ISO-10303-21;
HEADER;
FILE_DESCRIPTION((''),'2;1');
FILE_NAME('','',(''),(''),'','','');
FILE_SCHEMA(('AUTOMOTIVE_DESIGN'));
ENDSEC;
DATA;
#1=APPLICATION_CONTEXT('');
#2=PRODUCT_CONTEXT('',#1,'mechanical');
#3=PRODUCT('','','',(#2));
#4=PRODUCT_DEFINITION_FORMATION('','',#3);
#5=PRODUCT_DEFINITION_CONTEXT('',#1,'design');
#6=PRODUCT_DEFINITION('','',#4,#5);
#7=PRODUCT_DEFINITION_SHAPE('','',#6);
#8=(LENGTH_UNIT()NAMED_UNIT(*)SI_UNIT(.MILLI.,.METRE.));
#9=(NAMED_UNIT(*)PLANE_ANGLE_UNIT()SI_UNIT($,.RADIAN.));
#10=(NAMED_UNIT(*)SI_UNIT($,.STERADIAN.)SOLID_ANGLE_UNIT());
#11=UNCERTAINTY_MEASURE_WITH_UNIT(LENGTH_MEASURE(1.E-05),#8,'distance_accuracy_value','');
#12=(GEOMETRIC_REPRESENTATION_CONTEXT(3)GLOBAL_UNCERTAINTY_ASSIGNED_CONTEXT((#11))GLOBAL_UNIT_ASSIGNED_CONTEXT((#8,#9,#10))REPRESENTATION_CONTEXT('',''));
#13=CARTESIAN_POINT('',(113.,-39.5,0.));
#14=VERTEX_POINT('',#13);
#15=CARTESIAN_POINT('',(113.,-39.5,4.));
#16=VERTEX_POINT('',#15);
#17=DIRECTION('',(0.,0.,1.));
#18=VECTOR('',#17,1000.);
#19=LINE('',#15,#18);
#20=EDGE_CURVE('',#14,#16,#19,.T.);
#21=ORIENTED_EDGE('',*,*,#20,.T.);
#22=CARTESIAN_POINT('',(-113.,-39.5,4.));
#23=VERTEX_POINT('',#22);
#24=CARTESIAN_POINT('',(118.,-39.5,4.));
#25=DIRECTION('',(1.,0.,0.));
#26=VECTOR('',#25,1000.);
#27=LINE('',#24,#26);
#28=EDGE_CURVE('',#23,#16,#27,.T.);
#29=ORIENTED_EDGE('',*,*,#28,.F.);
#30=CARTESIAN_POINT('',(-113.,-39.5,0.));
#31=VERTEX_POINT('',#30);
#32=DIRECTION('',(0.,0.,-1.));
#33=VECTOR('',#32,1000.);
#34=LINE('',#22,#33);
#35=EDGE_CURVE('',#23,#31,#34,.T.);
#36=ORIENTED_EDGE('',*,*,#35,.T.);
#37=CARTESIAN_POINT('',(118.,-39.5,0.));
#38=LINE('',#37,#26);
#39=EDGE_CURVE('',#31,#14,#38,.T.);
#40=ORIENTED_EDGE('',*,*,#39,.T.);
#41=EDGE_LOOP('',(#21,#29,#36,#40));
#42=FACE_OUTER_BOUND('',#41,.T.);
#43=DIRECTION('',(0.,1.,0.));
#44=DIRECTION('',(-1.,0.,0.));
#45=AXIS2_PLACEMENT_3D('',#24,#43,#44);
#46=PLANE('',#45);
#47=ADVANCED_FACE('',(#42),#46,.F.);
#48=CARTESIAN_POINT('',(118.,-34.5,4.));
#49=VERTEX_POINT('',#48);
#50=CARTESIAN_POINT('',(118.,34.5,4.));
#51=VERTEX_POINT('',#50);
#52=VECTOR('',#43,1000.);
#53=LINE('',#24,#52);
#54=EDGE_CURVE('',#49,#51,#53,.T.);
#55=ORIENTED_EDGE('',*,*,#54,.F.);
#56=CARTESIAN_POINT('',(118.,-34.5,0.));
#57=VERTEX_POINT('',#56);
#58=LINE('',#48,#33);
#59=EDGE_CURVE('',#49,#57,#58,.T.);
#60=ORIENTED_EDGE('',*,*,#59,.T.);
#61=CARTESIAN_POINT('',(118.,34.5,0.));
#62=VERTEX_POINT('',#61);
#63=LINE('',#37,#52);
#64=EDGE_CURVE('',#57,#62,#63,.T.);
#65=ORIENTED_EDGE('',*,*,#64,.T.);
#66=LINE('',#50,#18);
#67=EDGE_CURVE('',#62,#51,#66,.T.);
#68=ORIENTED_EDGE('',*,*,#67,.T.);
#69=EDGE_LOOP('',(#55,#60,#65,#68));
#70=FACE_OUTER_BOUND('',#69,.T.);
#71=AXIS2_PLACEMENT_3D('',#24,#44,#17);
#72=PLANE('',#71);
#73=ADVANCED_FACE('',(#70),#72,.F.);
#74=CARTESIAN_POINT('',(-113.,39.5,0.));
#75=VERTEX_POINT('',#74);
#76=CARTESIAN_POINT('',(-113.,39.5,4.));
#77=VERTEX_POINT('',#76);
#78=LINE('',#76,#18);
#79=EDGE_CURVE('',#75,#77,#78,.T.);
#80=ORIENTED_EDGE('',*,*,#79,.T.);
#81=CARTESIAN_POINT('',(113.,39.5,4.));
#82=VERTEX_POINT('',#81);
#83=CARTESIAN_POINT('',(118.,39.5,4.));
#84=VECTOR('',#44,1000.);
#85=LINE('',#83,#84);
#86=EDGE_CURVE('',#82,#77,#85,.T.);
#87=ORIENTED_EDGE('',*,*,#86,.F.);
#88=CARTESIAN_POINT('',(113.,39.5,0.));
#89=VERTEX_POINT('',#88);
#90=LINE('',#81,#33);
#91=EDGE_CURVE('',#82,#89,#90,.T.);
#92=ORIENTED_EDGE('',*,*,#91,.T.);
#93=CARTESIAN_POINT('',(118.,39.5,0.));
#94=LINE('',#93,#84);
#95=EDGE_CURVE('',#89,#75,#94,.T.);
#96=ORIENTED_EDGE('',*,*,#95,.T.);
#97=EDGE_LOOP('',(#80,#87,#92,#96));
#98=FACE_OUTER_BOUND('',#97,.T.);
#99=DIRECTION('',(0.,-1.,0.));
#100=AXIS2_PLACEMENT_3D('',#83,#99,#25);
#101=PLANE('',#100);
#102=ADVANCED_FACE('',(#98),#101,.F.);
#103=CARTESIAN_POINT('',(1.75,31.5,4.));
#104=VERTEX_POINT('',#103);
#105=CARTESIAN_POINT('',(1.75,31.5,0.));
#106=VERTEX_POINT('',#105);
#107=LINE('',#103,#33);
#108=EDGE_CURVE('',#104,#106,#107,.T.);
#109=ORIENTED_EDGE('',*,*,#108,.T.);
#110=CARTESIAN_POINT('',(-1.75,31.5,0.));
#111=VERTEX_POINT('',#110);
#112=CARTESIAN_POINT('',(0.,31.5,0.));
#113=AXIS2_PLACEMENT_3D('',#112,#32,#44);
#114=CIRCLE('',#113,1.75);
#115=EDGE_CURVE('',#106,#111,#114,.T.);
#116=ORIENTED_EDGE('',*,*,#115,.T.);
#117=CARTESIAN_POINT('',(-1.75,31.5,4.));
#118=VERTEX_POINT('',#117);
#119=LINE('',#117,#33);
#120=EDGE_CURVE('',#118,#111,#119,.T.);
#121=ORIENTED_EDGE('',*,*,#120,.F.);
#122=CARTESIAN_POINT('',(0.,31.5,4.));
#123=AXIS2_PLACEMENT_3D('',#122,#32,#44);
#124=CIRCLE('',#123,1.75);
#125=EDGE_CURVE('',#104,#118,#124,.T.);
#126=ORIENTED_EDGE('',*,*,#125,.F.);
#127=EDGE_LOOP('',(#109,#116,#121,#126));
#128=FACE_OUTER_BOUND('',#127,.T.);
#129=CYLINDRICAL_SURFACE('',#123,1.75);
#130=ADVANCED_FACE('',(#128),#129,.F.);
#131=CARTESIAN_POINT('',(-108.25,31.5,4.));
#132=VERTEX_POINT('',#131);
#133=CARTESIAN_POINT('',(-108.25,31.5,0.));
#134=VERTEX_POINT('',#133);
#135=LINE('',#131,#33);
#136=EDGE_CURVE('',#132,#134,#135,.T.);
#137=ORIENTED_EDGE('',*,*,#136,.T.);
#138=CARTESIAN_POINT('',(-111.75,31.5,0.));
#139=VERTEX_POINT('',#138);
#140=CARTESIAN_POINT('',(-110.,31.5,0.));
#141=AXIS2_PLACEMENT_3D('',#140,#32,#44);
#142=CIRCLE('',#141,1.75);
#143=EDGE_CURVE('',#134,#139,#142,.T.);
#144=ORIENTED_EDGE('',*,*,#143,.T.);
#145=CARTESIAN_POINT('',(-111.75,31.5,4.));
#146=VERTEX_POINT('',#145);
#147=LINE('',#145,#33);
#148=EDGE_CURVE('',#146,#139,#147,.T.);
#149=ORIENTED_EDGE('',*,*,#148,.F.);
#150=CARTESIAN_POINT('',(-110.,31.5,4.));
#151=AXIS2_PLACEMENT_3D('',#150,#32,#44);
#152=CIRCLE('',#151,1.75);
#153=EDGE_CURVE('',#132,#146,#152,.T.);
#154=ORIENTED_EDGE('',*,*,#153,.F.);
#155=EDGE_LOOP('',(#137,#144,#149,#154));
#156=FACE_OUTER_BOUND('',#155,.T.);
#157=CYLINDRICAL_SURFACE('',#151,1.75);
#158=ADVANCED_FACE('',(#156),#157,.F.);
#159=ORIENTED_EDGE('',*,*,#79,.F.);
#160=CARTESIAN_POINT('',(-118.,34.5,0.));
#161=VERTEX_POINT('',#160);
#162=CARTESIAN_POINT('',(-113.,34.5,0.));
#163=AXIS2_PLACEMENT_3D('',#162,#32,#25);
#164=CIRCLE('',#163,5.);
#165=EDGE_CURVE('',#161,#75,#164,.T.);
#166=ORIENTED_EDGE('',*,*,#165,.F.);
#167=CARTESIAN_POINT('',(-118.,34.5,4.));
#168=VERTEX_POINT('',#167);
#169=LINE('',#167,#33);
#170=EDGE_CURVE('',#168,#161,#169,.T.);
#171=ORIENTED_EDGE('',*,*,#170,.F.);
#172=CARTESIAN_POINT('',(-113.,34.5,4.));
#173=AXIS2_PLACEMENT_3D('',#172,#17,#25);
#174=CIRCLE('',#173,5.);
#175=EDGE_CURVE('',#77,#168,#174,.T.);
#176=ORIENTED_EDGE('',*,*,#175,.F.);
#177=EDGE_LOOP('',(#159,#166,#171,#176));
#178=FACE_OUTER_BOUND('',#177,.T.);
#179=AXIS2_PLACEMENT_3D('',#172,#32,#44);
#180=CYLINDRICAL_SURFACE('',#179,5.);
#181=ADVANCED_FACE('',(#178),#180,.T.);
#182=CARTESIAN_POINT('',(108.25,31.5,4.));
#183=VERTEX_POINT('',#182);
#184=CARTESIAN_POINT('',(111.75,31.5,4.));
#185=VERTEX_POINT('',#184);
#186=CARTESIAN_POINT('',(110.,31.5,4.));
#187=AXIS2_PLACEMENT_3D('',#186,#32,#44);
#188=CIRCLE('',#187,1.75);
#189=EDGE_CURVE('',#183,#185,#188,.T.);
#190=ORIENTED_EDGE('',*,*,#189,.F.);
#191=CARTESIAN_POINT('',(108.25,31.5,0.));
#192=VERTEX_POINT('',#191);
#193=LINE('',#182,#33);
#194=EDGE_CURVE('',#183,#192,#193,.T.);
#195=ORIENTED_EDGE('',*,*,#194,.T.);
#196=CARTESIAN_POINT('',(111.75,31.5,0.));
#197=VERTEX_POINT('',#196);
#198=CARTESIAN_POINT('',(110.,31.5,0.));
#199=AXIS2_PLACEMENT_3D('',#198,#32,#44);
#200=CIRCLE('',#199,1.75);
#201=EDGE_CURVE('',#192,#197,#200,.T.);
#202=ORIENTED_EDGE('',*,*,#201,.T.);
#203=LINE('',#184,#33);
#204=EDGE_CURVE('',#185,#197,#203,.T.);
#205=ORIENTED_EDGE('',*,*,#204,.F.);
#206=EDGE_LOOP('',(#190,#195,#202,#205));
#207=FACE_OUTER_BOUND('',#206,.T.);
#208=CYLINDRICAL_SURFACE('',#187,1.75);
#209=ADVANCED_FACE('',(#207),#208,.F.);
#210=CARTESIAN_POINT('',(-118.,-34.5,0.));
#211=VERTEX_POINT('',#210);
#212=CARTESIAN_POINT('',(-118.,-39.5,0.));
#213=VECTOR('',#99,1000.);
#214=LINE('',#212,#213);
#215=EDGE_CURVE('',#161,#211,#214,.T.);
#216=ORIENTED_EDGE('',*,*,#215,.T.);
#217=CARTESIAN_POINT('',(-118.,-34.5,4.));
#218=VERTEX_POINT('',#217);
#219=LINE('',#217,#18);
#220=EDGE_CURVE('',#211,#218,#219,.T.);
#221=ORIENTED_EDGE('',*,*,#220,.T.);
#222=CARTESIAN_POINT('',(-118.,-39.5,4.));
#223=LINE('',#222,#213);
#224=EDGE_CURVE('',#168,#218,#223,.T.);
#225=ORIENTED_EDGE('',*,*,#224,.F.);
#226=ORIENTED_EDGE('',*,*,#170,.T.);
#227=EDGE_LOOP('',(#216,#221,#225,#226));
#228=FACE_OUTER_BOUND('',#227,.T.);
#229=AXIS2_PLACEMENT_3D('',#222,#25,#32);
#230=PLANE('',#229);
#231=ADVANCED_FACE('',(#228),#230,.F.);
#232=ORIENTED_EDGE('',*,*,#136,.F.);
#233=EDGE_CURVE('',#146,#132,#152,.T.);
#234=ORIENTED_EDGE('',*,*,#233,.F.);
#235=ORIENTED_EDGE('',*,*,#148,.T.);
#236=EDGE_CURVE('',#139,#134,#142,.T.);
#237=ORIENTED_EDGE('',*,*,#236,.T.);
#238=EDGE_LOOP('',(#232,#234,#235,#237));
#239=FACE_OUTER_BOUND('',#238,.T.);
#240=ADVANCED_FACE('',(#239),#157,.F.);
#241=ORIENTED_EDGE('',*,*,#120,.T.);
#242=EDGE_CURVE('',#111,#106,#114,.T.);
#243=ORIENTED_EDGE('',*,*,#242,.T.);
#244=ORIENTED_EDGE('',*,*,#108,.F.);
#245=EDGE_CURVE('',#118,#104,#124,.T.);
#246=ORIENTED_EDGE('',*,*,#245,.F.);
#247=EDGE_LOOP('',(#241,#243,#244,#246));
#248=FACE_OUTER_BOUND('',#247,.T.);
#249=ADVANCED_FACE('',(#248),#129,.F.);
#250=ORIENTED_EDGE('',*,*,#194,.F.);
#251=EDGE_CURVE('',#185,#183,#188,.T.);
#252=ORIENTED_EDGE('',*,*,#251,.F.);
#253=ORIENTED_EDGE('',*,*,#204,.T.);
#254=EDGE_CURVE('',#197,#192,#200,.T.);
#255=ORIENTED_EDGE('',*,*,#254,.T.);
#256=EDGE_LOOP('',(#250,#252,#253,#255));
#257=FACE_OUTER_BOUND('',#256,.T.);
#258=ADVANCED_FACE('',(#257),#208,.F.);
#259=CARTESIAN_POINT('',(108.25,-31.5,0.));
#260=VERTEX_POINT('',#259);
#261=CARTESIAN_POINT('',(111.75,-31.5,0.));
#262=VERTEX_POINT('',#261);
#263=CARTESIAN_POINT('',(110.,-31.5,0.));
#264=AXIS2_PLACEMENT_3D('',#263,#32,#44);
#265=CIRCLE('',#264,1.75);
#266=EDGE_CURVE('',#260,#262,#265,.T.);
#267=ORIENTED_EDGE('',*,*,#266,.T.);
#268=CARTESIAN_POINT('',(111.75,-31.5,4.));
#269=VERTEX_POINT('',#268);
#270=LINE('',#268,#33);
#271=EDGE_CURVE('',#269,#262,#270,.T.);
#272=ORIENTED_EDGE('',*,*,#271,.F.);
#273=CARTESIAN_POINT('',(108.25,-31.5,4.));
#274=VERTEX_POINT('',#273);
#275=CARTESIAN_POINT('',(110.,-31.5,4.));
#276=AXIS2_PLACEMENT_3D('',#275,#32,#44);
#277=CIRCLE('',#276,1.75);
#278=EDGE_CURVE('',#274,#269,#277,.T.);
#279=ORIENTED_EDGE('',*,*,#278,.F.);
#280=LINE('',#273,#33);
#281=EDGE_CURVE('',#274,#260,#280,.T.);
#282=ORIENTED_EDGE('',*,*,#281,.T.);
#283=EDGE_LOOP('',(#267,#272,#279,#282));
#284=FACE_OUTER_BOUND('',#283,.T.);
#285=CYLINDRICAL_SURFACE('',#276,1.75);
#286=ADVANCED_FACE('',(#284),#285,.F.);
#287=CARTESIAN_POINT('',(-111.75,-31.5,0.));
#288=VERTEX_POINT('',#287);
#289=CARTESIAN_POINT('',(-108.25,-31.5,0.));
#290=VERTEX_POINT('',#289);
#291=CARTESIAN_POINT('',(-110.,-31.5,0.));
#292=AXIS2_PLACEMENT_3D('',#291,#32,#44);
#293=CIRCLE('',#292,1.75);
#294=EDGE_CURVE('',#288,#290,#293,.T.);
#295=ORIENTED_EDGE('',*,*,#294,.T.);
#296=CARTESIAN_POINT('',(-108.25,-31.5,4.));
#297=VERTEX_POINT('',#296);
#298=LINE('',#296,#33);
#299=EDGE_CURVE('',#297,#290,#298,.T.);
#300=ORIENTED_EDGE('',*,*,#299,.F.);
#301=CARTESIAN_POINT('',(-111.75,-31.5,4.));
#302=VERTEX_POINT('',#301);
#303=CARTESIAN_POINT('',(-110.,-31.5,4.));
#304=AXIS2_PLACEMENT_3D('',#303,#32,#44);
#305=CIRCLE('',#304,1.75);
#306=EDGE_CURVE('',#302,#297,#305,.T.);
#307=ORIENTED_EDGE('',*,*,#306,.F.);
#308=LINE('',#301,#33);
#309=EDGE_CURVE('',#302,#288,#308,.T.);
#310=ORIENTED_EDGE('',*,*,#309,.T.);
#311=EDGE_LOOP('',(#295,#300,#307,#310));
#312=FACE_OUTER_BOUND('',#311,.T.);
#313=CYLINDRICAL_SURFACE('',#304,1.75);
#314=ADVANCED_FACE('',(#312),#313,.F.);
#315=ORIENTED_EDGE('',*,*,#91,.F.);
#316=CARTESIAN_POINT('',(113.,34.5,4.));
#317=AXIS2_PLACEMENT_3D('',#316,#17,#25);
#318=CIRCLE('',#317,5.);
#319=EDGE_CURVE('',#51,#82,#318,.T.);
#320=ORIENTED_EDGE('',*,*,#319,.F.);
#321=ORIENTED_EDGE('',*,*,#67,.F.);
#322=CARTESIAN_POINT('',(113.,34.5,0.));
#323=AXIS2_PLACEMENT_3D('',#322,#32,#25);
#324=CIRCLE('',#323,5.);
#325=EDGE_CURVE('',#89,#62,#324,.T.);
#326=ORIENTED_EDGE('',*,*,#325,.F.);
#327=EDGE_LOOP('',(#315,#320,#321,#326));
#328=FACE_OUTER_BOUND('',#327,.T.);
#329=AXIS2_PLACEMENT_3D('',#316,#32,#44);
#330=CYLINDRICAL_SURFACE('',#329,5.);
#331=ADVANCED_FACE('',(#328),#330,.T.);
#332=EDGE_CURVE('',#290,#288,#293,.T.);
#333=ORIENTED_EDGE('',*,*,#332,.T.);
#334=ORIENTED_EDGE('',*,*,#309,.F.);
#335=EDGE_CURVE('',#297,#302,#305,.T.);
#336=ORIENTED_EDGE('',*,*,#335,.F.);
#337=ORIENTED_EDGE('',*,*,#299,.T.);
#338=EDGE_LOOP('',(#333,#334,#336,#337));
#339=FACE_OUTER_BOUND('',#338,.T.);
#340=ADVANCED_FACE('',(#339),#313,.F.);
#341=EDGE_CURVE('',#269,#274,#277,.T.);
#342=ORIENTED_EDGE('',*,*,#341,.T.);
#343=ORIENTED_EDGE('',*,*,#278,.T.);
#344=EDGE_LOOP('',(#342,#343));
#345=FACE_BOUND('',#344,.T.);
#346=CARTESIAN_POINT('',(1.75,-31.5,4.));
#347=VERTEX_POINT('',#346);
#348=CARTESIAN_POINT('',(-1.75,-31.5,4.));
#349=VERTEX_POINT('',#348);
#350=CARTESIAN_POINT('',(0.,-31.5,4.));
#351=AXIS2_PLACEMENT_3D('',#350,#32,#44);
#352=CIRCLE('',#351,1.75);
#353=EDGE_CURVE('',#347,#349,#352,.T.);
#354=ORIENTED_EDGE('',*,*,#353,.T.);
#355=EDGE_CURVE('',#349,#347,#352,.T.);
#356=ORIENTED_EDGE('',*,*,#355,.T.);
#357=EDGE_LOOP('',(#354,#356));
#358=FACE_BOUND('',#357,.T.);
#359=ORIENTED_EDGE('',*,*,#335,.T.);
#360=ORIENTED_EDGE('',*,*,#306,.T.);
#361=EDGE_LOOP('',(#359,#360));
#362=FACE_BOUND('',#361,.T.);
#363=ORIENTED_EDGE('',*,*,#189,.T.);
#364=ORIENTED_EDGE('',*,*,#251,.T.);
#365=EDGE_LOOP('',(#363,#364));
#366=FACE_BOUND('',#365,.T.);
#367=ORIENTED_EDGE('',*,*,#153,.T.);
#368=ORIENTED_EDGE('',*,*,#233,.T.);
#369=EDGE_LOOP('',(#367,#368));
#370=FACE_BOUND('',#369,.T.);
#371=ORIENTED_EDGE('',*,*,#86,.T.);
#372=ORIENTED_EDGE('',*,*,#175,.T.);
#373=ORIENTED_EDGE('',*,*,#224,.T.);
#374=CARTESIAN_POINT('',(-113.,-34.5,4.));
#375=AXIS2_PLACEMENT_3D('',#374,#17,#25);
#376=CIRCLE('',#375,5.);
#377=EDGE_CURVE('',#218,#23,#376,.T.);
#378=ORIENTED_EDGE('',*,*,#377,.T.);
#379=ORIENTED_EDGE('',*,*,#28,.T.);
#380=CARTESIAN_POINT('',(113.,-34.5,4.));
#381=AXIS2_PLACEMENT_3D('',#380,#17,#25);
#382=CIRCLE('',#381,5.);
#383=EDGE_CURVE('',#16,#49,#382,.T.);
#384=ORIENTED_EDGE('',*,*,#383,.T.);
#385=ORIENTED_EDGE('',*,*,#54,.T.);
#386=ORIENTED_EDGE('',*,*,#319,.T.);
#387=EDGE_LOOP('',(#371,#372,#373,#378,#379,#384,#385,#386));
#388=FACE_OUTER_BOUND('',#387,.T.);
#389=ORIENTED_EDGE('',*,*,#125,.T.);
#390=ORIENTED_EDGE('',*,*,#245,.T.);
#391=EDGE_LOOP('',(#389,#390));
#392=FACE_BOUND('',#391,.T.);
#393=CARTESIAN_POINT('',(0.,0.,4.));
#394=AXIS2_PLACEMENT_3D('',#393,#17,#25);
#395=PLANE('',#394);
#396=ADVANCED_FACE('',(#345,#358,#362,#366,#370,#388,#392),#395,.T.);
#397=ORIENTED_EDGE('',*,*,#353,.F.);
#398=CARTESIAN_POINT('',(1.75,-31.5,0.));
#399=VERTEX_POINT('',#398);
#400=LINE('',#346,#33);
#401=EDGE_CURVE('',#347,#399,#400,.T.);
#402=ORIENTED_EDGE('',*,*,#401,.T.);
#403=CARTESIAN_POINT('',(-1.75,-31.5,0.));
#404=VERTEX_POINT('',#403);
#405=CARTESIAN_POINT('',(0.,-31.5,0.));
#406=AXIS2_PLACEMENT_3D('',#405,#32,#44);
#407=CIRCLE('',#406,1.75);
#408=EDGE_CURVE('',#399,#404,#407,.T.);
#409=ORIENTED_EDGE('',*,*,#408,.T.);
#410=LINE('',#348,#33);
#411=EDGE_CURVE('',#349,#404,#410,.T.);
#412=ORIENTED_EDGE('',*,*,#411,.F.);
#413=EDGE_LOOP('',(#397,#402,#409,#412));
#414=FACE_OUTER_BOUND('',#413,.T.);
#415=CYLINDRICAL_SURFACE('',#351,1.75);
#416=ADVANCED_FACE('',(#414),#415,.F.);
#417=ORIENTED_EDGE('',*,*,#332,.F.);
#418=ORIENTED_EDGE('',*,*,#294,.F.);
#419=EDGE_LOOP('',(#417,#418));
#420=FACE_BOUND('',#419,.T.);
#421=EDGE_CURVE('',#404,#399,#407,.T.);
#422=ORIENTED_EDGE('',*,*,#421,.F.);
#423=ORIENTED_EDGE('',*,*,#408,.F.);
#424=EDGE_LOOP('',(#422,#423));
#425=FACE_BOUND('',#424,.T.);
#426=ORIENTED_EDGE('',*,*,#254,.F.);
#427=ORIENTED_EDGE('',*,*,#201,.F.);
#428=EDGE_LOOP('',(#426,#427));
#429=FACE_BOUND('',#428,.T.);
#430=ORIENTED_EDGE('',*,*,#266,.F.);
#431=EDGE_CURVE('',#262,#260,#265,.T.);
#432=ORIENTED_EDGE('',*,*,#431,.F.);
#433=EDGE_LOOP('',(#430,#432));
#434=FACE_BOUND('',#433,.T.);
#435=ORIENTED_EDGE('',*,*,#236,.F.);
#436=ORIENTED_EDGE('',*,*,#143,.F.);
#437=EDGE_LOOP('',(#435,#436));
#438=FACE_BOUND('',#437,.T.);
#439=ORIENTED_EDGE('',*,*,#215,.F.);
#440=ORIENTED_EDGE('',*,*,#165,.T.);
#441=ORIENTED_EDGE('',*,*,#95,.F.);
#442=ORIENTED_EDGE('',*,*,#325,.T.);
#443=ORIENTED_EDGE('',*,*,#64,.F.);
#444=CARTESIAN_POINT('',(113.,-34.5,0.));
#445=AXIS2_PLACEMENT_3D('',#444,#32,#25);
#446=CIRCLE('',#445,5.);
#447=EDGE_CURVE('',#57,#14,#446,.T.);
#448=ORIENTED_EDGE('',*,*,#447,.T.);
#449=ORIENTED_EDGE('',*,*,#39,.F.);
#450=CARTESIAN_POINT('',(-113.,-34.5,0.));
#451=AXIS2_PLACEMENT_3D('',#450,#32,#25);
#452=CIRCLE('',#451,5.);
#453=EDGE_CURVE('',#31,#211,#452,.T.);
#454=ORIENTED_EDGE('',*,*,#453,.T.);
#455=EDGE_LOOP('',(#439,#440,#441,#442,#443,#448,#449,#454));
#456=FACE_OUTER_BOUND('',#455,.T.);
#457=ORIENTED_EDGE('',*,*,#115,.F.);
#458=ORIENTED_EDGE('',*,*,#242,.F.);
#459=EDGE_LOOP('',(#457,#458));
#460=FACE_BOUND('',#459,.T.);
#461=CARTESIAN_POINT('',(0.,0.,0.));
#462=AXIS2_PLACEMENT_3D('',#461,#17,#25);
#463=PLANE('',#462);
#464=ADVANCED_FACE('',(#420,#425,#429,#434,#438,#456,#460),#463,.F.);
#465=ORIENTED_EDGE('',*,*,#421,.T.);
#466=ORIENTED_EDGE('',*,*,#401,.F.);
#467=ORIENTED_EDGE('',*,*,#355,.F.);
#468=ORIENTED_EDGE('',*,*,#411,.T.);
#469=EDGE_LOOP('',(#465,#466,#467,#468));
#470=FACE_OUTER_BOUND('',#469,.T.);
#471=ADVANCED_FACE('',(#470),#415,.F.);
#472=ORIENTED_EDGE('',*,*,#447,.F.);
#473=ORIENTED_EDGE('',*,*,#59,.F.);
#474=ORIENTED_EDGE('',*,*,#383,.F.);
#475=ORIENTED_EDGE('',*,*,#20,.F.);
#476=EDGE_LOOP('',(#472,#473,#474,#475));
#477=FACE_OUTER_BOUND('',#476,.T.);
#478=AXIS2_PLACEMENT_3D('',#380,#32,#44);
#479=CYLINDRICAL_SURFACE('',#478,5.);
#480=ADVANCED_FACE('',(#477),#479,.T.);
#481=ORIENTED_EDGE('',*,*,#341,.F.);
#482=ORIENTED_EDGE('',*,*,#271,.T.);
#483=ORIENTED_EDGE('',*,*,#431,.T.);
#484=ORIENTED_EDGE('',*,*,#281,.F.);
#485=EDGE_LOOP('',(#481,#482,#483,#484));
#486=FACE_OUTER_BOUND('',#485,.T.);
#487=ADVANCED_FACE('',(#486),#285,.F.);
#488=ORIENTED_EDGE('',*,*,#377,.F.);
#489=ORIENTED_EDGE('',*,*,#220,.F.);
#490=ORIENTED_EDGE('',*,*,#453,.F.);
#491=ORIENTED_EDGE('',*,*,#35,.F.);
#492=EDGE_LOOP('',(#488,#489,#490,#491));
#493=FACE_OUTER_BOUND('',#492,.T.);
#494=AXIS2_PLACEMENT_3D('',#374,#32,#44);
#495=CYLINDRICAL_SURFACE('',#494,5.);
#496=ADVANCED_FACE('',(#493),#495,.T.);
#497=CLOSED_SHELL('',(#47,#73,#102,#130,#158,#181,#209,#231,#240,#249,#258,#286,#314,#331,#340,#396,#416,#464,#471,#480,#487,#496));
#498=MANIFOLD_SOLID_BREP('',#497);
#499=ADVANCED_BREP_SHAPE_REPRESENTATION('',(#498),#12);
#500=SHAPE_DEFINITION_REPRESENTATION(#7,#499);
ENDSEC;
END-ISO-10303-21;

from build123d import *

# Parameters (mm, degrees)
SKETCH1_W           = 236
SKETCH1_H           = 79
BOSS_EXTRUDE1_DEPTH = 4
FILLET1_R           = 5
SKETCH4_R           = 1.75
CUT_EXTRUDE1_DEPTH  = 125.5


with BuildPart() as part:
    # Sketch1 → Boss-Extrude1 (new body)
    with BuildSketch(Plane.XY):
        Rectangle(SKETCH1_W, SKETCH1_H)
    extrude(amount=BOSS_EXTRUDE1_DEPTH)

    # Fillet1
    fillet1_edges = [part.edges().sort_by_distance(p)[0] for p in [
        (-118, 39.5, 2),
        (118, 39.5, 2),
        (118, -39.5, 2),
        (-118, -39.5, 2),
    ]]
    fillet(fillet1_edges, radius=FILLET1_R)

    # Sketch4 → Cut-Extrude1 (cut, through all)
    with BuildSketch(Plane(origin=(0, 0, 0), x_dir=(-1, 0, 0), z_dir=(0, 0, -1))):
        with Locations((-110, 31.5)):
            Circle(SKETCH4_R)
        with Locations((110, 31.5)):
            Circle(SKETCH4_R)
        with Locations((110, -31.5)):
            Circle(SKETCH4_R)
        with Locations((-110, -31.5)):
            Circle(SKETCH4_R)
        with Locations((0, 31.5)):
            Circle(SKETCH4_R)
        with Locations((0, -31.5)):
            Circle(SKETCH4_R)
    extrude(amount=-CUT_EXTRUDE1_DEPTH, mode=Mode.SUBTRACT)


solid = part.part
